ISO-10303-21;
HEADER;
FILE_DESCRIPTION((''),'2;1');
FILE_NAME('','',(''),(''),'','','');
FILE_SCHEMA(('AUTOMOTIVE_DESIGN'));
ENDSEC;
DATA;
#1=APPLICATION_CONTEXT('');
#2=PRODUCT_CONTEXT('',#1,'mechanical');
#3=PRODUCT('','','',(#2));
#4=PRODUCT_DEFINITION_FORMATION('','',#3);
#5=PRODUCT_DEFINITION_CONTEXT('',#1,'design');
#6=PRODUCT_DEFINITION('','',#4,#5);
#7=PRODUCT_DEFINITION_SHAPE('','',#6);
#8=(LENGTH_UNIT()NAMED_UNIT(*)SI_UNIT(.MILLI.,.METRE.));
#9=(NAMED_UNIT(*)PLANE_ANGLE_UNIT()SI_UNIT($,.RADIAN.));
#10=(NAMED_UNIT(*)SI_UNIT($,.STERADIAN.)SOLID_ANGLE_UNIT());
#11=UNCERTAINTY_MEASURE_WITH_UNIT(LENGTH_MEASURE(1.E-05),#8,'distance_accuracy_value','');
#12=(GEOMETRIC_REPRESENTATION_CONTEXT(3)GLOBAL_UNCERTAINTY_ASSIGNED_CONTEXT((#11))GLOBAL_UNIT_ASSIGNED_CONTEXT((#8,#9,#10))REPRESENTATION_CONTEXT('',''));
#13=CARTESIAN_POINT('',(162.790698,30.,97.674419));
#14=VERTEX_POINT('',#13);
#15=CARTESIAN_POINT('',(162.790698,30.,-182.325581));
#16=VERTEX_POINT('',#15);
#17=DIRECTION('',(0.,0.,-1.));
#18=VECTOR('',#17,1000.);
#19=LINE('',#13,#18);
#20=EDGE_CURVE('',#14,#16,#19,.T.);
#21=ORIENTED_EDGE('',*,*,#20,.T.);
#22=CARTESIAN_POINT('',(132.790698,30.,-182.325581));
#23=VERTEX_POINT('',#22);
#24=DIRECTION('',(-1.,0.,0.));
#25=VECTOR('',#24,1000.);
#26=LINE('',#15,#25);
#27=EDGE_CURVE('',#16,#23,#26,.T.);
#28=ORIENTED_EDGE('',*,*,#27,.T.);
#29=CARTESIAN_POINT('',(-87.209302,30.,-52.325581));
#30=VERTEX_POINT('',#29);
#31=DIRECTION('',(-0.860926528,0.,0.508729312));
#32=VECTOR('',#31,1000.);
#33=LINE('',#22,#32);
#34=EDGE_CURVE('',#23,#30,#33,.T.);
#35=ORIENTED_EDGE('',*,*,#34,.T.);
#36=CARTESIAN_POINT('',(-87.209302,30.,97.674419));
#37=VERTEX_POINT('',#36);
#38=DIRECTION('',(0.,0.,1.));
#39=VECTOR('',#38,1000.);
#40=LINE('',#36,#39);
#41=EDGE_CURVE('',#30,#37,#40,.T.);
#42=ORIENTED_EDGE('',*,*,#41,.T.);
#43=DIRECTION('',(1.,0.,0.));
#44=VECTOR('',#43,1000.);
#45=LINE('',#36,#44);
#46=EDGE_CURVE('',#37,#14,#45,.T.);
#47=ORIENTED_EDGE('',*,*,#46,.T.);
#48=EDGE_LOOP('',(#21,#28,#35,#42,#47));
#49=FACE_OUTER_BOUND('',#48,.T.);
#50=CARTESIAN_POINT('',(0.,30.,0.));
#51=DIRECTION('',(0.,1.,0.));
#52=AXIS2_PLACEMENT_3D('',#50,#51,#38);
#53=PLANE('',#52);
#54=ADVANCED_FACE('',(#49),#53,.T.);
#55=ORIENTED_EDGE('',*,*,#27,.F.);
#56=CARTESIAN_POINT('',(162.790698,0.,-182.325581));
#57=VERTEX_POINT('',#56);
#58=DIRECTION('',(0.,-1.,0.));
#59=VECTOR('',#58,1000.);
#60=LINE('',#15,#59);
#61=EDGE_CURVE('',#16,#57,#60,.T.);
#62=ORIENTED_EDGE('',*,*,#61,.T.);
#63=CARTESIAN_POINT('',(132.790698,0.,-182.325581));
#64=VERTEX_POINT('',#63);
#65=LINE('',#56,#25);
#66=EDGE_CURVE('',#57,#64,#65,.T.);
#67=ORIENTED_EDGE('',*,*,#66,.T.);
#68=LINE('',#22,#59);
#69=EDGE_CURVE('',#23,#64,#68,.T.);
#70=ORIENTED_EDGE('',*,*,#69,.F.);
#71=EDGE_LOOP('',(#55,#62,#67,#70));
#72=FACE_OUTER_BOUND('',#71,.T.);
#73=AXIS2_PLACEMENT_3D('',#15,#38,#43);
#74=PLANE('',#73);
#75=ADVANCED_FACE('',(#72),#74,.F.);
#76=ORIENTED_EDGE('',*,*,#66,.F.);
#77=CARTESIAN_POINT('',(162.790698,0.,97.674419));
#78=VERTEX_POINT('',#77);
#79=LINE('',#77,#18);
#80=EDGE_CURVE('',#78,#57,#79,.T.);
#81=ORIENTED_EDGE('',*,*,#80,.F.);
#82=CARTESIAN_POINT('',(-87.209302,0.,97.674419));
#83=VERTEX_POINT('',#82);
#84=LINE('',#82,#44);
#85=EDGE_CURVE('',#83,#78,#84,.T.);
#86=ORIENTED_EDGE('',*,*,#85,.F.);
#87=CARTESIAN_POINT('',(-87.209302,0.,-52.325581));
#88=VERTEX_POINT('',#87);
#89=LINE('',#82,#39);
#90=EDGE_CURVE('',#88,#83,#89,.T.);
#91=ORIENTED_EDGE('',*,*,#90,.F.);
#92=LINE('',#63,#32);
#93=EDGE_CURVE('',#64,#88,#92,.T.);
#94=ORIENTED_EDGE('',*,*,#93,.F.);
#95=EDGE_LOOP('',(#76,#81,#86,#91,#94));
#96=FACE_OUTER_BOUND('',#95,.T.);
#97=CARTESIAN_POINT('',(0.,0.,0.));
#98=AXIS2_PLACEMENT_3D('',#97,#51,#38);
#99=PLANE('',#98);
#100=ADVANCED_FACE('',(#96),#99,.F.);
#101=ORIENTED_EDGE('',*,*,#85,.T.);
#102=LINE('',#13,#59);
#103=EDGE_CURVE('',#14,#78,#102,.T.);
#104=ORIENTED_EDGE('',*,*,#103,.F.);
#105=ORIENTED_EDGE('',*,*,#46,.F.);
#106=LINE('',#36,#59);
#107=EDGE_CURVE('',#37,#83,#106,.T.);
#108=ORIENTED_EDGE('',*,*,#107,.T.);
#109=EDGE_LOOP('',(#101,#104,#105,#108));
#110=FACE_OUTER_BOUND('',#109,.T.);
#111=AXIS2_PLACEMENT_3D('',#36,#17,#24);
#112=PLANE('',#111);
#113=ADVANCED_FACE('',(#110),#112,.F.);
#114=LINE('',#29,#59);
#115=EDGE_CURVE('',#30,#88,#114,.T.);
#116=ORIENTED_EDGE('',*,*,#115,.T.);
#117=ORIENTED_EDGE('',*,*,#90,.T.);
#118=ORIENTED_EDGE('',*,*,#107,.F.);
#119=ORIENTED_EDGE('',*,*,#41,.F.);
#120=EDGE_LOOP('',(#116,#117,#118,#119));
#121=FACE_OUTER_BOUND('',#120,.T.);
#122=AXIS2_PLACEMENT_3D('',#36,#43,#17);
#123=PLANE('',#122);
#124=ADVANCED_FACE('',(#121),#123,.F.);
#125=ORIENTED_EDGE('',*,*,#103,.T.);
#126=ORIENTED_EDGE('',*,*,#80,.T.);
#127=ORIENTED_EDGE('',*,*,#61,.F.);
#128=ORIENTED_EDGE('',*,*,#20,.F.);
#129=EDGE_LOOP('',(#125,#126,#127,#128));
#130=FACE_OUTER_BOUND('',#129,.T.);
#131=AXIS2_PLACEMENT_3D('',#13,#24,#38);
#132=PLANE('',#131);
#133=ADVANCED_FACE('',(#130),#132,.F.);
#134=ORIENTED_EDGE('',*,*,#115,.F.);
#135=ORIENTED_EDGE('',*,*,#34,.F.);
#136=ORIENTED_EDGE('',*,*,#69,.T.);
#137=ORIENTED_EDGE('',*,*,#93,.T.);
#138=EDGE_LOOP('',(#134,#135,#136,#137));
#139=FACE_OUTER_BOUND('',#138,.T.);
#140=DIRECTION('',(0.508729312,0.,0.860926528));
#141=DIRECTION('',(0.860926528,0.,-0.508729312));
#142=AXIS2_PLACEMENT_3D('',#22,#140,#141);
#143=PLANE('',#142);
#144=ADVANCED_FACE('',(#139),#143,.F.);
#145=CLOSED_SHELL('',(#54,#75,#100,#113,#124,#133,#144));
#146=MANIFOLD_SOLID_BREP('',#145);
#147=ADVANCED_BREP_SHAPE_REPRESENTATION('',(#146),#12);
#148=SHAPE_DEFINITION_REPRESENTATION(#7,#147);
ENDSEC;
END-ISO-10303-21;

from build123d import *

# Parameters (mm, degrees)
EXTRUDE_1_DEPTH = 30


with BuildPart() as part:
    # 草图1 → 凸台-拉伸1 (new body)
    with BuildSketch(Plane(origin=(0, 0, 0), x_dir=(1, 0, 0), z_dir=(0, 1, 0))):
        Polygon((162.790697674, 182.325581395), (132.790697674, 182.325581395), (-87.209302326, 52.325581395), (-87.209302326, -97.674418605), (162.790697674, -97.674418605), align=None)
    extrude(amount=EXTRUDE_1_DEPTH)


solid = part.part
